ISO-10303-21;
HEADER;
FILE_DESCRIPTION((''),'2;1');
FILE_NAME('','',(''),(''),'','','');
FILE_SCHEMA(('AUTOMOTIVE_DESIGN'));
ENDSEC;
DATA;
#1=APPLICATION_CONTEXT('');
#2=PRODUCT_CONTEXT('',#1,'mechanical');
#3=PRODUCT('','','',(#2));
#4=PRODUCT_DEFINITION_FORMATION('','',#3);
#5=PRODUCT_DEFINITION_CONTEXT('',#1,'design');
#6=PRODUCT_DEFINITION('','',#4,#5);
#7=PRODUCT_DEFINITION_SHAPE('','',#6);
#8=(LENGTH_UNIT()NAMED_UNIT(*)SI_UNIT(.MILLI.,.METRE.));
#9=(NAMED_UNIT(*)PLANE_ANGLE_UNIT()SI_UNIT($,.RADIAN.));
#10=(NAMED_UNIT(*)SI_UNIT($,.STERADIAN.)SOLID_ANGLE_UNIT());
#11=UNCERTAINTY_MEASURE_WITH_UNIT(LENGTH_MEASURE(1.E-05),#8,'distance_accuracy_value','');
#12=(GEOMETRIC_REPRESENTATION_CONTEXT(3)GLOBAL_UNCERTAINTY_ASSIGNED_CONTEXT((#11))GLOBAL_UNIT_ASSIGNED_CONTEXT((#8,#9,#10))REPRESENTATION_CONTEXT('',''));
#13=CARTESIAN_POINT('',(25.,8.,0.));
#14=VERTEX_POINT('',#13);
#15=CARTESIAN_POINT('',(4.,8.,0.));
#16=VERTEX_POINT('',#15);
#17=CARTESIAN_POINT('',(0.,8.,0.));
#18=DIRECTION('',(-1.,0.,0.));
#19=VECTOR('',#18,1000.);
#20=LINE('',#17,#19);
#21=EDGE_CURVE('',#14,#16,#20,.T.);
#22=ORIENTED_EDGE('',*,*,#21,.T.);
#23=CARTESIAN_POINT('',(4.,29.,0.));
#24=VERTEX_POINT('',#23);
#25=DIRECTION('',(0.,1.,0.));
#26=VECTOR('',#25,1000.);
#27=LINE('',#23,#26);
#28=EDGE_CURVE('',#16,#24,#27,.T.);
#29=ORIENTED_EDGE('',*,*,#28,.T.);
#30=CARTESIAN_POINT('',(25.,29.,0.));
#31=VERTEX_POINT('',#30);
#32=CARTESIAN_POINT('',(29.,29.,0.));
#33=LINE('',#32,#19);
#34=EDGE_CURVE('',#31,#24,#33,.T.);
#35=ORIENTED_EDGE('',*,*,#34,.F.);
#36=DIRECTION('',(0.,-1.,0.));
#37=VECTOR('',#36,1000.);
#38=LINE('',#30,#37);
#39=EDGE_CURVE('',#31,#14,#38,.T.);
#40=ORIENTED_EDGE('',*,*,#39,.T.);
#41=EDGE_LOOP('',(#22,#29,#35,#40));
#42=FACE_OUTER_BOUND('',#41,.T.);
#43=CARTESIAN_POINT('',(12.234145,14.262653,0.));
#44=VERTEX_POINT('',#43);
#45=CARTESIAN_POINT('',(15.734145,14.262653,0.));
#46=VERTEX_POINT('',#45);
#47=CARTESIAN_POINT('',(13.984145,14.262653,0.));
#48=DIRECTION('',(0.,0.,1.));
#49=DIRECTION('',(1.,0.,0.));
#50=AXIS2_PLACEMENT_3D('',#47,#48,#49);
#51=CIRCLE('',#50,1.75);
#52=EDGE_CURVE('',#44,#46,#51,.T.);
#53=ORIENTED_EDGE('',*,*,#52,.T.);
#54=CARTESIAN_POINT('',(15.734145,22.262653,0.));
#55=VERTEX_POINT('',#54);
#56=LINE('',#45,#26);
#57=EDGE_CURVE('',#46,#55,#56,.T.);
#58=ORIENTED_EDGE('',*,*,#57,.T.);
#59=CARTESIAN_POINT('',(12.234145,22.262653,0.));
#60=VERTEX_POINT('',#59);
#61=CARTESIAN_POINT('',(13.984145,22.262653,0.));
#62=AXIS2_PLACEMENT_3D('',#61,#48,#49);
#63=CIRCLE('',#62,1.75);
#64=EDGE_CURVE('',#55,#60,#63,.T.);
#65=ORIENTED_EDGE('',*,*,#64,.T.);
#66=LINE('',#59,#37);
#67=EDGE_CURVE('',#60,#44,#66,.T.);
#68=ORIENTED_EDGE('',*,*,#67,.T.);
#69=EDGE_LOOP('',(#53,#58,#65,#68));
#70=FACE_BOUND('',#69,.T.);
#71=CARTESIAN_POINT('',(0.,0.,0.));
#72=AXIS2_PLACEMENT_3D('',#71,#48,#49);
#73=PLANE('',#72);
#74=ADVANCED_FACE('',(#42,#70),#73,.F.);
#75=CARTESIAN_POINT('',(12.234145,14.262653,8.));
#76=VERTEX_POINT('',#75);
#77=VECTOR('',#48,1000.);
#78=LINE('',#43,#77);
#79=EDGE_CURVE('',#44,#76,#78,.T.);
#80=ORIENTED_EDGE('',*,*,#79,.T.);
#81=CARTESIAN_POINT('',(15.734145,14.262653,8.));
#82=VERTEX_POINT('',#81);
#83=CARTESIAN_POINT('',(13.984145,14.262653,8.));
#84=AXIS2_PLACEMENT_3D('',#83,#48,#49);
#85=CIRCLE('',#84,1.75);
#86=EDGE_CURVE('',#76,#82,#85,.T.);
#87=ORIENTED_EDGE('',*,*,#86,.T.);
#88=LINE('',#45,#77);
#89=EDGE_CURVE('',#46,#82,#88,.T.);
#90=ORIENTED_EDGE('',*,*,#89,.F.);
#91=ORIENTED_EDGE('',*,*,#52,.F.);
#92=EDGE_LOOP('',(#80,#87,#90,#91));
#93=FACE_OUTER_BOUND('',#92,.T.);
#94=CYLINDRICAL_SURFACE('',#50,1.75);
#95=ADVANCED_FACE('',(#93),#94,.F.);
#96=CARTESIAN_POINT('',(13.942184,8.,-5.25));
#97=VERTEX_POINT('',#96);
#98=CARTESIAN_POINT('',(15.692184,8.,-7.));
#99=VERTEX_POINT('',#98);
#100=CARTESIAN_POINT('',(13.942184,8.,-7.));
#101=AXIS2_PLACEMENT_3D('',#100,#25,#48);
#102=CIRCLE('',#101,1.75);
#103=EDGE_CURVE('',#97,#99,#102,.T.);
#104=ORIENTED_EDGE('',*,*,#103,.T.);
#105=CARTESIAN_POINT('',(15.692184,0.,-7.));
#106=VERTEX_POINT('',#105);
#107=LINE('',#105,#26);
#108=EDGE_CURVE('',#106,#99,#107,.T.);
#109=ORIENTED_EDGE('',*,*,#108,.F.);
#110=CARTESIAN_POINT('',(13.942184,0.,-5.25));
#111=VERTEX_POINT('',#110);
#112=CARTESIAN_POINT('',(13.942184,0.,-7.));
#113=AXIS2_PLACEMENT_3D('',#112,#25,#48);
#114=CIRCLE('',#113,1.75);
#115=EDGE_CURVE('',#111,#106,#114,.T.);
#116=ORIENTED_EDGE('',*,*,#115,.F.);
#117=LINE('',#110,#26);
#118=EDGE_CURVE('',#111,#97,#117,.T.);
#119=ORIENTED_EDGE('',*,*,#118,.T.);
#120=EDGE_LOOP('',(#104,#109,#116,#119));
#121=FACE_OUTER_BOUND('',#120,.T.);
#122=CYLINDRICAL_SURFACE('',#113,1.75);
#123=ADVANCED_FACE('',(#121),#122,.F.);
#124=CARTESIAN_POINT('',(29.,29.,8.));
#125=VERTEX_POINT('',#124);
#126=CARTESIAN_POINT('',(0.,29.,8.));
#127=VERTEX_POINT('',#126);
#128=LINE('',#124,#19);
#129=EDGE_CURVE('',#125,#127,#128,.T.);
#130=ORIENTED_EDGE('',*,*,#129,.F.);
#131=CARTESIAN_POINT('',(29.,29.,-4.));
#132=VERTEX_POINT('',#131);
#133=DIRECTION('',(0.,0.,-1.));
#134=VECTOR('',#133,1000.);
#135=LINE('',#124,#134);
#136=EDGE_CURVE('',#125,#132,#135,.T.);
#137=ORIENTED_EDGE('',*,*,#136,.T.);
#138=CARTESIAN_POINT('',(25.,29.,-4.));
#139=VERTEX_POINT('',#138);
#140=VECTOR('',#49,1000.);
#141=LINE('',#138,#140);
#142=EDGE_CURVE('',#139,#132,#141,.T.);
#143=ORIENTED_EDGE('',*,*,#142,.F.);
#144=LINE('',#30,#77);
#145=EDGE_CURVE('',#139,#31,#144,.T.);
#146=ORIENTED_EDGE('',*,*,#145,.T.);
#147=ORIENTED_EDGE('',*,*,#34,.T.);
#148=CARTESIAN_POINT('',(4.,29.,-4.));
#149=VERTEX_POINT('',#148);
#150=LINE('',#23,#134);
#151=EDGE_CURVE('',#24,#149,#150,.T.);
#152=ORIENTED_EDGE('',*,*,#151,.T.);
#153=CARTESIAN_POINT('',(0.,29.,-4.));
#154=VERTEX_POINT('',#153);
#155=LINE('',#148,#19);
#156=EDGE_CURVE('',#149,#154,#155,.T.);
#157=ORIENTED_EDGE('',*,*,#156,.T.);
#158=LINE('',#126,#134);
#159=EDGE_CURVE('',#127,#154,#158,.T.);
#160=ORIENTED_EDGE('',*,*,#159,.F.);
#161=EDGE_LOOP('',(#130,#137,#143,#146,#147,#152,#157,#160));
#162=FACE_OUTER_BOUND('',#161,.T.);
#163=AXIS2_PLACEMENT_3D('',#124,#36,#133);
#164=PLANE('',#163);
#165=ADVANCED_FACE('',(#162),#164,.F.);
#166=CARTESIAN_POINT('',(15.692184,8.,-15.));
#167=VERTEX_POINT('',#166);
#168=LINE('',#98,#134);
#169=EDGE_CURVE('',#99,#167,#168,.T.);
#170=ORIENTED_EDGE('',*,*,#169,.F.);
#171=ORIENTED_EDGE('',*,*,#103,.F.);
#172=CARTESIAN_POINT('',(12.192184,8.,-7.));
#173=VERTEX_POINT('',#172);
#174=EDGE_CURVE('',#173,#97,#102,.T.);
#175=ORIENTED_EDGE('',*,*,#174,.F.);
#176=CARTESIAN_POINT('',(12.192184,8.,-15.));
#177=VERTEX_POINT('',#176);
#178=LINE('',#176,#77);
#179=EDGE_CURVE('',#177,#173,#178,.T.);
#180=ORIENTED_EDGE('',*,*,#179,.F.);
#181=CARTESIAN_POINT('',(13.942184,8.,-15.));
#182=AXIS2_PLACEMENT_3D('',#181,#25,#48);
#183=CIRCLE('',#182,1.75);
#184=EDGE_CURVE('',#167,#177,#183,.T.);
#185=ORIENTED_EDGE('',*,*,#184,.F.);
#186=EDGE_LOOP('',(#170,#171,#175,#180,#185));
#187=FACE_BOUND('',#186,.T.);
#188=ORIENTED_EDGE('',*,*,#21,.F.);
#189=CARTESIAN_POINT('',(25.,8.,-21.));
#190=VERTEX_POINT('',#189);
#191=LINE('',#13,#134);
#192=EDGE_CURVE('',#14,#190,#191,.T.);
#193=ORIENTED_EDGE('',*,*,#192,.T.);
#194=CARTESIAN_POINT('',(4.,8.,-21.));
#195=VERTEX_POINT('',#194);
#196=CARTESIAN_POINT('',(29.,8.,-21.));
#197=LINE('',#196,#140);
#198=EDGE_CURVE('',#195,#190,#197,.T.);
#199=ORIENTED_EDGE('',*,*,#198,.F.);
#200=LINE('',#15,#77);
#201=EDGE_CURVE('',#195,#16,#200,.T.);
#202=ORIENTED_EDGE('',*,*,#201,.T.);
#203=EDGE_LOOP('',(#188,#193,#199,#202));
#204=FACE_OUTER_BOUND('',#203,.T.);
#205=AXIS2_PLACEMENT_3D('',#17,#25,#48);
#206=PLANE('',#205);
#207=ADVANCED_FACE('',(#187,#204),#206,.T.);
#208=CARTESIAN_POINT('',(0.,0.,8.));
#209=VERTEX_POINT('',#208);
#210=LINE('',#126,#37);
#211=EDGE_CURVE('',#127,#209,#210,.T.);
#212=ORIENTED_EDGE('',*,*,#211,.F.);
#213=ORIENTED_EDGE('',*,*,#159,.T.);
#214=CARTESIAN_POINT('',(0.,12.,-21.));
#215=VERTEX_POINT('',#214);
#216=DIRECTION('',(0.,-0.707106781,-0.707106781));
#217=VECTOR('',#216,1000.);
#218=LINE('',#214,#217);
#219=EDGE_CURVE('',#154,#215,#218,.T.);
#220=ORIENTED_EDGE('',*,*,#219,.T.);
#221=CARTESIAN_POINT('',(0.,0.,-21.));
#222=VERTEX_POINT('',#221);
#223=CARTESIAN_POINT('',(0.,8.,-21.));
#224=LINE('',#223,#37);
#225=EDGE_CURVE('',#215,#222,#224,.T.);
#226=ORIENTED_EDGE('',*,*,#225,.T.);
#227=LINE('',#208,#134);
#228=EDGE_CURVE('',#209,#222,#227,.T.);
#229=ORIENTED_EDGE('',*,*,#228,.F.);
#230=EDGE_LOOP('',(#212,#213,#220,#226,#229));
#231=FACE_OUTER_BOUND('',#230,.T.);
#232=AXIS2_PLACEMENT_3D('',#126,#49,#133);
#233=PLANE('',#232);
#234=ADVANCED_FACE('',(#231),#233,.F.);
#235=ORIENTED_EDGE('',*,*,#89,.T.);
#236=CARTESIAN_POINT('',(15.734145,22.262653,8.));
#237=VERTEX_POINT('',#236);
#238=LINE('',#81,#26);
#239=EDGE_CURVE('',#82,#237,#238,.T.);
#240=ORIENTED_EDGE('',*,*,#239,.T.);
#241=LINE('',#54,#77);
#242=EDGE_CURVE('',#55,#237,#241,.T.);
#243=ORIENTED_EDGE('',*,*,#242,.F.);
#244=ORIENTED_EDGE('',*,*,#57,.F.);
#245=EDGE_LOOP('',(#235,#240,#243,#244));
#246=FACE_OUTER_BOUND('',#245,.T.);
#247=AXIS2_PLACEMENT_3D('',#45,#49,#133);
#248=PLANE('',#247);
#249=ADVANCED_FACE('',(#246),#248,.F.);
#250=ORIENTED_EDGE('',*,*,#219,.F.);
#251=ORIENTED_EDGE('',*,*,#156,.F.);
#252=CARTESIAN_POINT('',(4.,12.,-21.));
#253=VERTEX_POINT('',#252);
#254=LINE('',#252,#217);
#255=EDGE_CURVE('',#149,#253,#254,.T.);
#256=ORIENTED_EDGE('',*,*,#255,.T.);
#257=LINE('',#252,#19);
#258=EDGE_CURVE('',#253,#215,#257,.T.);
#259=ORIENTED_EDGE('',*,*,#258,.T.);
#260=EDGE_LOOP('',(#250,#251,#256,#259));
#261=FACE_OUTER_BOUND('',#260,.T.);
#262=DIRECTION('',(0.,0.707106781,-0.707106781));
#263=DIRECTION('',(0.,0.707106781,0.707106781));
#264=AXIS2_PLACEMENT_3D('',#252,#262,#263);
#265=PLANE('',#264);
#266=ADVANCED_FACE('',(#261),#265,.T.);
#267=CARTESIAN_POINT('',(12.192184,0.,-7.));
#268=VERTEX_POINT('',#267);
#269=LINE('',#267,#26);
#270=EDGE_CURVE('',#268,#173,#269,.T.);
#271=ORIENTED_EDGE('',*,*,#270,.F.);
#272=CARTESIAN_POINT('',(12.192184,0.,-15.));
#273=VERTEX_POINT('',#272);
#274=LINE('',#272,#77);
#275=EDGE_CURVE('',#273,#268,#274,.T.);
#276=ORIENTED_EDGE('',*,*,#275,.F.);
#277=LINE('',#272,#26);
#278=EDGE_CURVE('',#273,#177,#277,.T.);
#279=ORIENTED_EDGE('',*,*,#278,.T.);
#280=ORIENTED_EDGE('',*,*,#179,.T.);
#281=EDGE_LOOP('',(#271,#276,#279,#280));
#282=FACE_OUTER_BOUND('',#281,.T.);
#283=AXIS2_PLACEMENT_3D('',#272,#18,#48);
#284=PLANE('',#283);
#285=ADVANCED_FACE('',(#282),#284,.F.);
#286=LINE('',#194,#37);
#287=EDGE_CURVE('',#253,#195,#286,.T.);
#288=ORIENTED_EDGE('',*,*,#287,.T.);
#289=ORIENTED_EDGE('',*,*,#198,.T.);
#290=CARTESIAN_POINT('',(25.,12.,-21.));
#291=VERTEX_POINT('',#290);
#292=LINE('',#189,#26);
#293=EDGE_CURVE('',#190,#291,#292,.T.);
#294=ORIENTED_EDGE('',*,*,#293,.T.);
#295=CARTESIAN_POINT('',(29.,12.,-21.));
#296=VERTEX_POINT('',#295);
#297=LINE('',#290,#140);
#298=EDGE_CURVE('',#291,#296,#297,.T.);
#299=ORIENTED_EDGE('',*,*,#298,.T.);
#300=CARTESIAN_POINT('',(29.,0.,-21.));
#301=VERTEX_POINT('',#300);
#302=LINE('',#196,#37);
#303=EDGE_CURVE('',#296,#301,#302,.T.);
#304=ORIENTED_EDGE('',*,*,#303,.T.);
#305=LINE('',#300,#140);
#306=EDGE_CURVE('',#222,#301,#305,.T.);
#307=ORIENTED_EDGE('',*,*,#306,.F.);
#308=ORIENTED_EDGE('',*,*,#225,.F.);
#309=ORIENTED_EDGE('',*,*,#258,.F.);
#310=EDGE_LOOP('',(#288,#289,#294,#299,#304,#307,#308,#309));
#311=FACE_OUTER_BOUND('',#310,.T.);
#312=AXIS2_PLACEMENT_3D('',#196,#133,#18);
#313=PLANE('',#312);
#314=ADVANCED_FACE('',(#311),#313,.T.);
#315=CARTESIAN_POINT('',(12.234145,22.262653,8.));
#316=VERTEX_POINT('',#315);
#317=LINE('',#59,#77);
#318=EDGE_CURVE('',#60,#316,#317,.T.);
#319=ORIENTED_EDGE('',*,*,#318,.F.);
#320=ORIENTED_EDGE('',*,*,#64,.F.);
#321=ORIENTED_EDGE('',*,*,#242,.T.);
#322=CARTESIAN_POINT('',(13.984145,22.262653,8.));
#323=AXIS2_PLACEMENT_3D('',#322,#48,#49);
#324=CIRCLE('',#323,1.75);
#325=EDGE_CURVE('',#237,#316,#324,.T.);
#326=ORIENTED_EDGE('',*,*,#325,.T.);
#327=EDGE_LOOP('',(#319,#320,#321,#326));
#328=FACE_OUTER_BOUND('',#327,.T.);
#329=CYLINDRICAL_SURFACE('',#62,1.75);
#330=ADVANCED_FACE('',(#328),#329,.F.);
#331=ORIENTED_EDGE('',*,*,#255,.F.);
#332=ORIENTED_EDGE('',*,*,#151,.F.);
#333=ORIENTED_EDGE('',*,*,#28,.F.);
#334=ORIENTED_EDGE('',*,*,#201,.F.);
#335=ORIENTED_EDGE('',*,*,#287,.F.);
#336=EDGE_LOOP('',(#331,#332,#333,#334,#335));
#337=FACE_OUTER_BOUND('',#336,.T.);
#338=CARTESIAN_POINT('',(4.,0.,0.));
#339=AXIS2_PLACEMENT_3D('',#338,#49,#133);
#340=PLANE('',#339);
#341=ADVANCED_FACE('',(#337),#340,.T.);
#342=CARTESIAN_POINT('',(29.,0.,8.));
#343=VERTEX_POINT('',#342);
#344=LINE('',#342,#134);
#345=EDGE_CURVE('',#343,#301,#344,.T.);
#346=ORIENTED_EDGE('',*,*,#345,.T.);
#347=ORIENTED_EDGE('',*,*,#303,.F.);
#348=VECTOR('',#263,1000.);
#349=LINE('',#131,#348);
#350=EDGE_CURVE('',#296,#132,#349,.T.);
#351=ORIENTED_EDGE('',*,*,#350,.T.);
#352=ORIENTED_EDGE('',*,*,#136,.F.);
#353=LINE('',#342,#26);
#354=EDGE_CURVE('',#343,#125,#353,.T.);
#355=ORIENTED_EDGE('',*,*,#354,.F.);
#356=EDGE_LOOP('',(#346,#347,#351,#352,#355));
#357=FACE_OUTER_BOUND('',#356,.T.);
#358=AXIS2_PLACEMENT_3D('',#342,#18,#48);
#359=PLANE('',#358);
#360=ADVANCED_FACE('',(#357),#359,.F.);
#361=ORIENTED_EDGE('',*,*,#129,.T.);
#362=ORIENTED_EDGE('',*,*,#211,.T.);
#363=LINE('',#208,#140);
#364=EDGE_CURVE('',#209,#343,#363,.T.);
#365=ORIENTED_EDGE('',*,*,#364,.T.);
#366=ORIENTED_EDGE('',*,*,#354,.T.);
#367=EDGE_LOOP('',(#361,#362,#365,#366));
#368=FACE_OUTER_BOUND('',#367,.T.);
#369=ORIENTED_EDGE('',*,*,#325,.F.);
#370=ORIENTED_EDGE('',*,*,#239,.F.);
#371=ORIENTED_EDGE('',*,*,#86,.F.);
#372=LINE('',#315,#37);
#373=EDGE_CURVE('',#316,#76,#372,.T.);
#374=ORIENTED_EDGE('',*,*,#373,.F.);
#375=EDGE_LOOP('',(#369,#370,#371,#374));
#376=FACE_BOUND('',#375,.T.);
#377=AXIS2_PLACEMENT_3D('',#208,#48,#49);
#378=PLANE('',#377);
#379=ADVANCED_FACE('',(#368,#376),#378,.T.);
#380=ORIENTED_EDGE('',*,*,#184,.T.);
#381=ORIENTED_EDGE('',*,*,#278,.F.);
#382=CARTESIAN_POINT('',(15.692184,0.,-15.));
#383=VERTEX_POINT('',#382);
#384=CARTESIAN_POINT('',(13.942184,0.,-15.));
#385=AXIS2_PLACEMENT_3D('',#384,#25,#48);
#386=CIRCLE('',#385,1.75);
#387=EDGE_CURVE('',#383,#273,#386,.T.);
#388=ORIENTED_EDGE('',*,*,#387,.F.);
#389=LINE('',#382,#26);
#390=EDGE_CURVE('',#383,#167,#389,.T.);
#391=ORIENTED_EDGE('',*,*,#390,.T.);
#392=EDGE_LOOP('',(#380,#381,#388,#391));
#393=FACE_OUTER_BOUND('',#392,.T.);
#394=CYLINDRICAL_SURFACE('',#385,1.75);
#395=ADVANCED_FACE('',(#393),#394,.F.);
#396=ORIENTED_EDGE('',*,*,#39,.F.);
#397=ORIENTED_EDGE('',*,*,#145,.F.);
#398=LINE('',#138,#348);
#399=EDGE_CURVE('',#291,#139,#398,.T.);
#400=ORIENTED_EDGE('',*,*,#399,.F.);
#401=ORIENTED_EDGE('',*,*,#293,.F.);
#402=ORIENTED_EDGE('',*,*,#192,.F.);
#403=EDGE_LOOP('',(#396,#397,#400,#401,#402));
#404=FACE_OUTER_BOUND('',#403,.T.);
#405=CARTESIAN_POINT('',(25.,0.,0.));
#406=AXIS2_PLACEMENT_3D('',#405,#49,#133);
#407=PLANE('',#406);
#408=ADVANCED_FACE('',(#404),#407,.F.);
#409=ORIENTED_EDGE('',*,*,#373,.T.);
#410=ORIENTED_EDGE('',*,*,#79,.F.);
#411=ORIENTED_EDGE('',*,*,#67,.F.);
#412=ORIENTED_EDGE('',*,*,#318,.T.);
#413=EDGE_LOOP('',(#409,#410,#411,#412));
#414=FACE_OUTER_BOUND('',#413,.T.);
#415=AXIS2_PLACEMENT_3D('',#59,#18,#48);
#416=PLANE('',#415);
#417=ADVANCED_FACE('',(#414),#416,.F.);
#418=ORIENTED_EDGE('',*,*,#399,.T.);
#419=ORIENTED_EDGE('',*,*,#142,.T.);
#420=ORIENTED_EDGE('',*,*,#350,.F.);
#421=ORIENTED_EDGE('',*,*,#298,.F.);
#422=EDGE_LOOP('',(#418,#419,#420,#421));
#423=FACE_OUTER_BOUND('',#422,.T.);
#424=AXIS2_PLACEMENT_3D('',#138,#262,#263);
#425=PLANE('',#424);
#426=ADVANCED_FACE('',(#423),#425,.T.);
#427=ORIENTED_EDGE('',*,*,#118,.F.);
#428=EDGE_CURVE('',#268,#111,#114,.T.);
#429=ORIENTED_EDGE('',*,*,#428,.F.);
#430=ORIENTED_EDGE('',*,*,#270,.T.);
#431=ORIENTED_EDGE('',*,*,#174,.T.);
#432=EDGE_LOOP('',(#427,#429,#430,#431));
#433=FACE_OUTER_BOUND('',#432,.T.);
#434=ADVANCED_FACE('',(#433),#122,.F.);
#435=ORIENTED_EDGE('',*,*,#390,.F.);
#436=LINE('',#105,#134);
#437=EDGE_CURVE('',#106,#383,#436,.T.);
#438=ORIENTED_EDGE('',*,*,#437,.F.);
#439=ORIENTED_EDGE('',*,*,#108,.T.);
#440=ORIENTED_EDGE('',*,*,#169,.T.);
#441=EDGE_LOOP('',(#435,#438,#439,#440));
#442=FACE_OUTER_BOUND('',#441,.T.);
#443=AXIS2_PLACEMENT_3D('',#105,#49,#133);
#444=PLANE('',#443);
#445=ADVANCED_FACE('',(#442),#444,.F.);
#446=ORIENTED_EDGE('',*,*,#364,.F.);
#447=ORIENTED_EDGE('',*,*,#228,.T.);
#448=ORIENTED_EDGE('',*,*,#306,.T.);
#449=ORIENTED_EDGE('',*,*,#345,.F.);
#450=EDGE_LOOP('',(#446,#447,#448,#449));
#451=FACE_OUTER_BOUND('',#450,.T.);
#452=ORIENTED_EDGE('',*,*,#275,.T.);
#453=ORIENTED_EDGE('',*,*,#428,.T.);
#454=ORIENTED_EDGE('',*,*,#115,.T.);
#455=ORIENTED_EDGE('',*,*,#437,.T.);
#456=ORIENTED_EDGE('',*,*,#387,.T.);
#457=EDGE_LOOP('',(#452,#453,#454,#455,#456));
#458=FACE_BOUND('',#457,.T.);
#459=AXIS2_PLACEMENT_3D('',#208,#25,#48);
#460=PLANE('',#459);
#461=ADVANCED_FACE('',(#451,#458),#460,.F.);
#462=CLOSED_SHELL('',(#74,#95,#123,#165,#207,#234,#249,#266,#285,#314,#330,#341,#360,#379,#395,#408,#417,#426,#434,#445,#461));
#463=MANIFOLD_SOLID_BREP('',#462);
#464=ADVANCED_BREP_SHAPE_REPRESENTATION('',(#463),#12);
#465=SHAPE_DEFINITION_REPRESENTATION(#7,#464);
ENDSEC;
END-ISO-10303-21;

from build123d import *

# Parameters (mm, degrees)
BASE_PLATE_SKETCH_W    = 29
BASE_PLATE_SKETCH_H    = 29
BASE_PLATE_8MM_DEPTH   = 8
BASE_SLOT_3_5MM_DEPTH  = 8
UPRIGHT_WALL_SKETCH_W  = 29
UPRIGHT_WALL_SKETCH_H  = 21
UPRIGHT_WALL_8MM_DEPTH = 8
WALL_SLOT_3_5MM_DEPTH  = 8
SIDE_BOSS_A_4MM_DEPTH  = 4
SIDE_BOSS_B_4MM_DEPTH  = 4


with BuildPart() as part:
    # Base Plate Sketch → Base Plate 8mm (new body)
    with BuildSketch(Plane.XY):
        with Locations((14.5, 14.5)):
            Rectangle(BASE_PLATE_SKETCH_W, BASE_PLATE_SKETCH_H)
    extrude(amount=BASE_PLATE_8MM_DEPTH)

    # Base Slot Sketch → Base Slot 3.5mm (cut)
    with BuildSketch(Plane.XY.offset(8)):
        with BuildLine():
            Line((12.234144505, 22.262653084), (12.234144505, 14.262653084))
            ThreePointArc((12.234144505, 14.262653084), (13.984144505, 12.512653084), (15.734144505, 14.262653084))
            Line((15.734144505, 14.262653084), (15.734144505, 22.262653084))
            ThreePointArc((15.734144505, 22.262653084), (13.984144505, 24.012653084), (12.234144505, 22.262653084))
        make_face()
    extrude(amount=-BASE_SLOT_3_5MM_DEPTH, mode=Mode.SUBTRACT)

    # Upright Wall Sketch → Upright Wall 8mm (add)
    with BuildSketch(Plane.XZ):
        with Locations((14.5, -10.5)):
            Rectangle(UPRIGHT_WALL_SKETCH_W, UPRIGHT_WALL_SKETCH_H)
    extrude(amount=-UPRIGHT_WALL_8MM_DEPTH)

    # Wall Slot Sketch → Wall Slot 3.5mm (cut)
    with BuildSketch(Plane(origin=(0, 8, 0), x_dir=(1, 0, 0), z_dir=(0, 1, 0))):
        with BuildLine():
            Line((12.192184218, 15), (12.192184218, 7))
            ThreePointArc((12.192184218, 7), (13.942184218, 5.25), (15.692184218, 7))
            Line((15.692184218, 7), (15.692184218, 15))
            ThreePointArc((15.692184218, 15), (13.942184218, 16.75), (12.192184218, 15))
        make_face()
    extrude(amount=-WALL_SLOT_3_5MM_DEPTH, mode=Mode.SUBTRACT)

    # Side Boss A Sketch → Side Boss A 4mm (add)
    with BuildSketch(Plane(origin=(29, 0, 0), x_dir=(0, 0, -1), z_dir=(1, 0, 0))):
        Polygon((0, 29), (4, 29), (21, 12), (21, 8), (0, 8), align=None)
    extrude(amount=-SIDE_BOSS_A_4MM_DEPTH)

    # Side Boss B Sketch → Side Boss B 4mm (add)
    with BuildSketch(Plane.ZY):
        Polygon((0, 29), (-4, 29), (-21, 12), (-21, 8), (0, 8), align=None)
    extrude(amount=-SIDE_BOSS_B_4MM_DEPTH)


solid = part.part
